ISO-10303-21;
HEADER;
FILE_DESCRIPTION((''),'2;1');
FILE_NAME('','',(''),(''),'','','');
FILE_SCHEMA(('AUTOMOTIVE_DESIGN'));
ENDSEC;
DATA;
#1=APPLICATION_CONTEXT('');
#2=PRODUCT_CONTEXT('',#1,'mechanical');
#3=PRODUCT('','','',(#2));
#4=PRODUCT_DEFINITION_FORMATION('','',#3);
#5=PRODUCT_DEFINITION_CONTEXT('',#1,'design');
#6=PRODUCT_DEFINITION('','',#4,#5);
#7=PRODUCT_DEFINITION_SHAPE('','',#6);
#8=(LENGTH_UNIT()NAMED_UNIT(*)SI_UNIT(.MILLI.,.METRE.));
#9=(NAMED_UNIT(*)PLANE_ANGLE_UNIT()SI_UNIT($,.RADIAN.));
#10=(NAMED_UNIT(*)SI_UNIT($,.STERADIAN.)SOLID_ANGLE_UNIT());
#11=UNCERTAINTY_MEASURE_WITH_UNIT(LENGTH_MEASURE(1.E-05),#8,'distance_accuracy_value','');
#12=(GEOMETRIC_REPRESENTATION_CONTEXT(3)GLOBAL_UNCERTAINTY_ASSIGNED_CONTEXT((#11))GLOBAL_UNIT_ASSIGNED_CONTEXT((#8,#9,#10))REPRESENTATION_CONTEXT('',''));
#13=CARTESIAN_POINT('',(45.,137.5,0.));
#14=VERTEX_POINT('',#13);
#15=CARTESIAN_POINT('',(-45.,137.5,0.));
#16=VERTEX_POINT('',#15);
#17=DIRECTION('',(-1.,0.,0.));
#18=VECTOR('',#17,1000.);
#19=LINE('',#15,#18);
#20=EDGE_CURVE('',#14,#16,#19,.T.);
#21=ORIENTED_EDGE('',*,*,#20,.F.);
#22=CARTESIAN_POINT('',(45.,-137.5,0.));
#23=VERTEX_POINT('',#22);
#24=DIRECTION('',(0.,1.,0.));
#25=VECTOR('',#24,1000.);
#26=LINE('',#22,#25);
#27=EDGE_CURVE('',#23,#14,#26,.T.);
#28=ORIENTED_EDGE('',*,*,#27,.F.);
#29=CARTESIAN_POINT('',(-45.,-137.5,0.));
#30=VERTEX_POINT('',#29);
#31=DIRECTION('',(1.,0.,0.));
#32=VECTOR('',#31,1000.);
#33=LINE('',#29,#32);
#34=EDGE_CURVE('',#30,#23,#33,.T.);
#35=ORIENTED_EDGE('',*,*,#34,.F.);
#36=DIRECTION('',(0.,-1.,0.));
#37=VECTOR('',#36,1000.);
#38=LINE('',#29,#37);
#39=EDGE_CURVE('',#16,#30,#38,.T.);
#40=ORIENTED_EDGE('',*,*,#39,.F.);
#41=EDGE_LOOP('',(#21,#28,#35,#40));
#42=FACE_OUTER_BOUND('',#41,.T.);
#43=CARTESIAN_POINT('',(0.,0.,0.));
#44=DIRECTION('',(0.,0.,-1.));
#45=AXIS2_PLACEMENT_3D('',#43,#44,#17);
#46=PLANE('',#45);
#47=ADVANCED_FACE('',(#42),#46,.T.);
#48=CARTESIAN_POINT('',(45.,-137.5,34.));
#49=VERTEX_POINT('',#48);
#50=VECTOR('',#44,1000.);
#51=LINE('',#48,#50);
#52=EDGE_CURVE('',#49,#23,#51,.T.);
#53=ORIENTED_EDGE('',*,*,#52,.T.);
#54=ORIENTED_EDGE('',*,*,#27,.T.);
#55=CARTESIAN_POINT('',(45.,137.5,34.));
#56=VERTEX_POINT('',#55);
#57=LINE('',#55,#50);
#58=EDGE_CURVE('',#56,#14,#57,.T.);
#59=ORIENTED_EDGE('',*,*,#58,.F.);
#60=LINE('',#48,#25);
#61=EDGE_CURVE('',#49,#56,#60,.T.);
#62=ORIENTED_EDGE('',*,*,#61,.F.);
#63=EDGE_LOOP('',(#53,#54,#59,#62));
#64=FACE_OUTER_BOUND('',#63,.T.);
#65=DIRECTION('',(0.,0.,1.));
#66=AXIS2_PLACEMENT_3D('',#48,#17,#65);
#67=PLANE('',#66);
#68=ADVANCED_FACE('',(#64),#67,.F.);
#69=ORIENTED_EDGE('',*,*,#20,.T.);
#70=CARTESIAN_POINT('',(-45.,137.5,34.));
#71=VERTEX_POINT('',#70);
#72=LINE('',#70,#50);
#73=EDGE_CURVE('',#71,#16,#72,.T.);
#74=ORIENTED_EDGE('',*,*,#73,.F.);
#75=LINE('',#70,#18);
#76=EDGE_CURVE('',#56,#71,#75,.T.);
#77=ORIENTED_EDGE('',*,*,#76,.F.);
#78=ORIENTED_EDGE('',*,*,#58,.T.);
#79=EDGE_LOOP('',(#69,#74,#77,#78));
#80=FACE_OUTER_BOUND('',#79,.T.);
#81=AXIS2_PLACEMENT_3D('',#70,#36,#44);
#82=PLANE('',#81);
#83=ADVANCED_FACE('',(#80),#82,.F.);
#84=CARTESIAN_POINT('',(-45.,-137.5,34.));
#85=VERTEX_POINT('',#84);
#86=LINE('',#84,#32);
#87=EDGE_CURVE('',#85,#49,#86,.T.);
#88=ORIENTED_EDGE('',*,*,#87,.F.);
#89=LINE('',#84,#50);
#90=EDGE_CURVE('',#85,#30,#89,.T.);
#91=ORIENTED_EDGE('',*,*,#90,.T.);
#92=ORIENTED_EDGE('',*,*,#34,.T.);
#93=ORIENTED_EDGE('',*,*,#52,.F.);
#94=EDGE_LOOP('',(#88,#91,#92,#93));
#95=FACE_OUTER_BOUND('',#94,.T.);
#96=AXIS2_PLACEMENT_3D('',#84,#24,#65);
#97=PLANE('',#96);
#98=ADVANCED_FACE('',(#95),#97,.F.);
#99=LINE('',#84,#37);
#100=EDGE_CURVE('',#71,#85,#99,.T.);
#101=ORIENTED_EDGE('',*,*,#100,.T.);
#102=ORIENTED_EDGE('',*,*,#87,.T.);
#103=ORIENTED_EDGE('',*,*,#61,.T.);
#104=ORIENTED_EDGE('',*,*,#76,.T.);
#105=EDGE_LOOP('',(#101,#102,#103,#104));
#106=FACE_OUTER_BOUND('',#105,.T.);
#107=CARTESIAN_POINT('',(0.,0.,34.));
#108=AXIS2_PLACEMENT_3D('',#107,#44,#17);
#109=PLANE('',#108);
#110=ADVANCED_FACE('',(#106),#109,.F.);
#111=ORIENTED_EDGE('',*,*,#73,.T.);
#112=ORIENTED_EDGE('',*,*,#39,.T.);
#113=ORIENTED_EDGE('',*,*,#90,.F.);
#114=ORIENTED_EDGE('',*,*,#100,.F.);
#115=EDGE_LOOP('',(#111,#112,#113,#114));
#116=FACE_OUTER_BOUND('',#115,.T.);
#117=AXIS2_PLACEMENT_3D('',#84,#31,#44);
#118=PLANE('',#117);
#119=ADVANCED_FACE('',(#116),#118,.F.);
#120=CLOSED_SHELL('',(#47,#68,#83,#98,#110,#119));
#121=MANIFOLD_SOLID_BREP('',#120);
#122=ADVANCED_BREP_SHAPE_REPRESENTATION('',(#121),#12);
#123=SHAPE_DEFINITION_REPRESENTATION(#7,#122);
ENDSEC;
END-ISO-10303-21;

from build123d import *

# Parameters (mm, degrees)
SKETCH_1_W      = 90
SKETCH_1_H      = 275
EXTRUDE_1_DEPTH = 34


with BuildPart() as part:
    # 草图1 → 凸台-拉伸1 (new body)
    with BuildSketch(Plane.XY):
        Rectangle(SKETCH_1_W, SKETCH_1_H)
    extrude(amount=EXTRUDE_1_DEPTH)


solid = part.part
